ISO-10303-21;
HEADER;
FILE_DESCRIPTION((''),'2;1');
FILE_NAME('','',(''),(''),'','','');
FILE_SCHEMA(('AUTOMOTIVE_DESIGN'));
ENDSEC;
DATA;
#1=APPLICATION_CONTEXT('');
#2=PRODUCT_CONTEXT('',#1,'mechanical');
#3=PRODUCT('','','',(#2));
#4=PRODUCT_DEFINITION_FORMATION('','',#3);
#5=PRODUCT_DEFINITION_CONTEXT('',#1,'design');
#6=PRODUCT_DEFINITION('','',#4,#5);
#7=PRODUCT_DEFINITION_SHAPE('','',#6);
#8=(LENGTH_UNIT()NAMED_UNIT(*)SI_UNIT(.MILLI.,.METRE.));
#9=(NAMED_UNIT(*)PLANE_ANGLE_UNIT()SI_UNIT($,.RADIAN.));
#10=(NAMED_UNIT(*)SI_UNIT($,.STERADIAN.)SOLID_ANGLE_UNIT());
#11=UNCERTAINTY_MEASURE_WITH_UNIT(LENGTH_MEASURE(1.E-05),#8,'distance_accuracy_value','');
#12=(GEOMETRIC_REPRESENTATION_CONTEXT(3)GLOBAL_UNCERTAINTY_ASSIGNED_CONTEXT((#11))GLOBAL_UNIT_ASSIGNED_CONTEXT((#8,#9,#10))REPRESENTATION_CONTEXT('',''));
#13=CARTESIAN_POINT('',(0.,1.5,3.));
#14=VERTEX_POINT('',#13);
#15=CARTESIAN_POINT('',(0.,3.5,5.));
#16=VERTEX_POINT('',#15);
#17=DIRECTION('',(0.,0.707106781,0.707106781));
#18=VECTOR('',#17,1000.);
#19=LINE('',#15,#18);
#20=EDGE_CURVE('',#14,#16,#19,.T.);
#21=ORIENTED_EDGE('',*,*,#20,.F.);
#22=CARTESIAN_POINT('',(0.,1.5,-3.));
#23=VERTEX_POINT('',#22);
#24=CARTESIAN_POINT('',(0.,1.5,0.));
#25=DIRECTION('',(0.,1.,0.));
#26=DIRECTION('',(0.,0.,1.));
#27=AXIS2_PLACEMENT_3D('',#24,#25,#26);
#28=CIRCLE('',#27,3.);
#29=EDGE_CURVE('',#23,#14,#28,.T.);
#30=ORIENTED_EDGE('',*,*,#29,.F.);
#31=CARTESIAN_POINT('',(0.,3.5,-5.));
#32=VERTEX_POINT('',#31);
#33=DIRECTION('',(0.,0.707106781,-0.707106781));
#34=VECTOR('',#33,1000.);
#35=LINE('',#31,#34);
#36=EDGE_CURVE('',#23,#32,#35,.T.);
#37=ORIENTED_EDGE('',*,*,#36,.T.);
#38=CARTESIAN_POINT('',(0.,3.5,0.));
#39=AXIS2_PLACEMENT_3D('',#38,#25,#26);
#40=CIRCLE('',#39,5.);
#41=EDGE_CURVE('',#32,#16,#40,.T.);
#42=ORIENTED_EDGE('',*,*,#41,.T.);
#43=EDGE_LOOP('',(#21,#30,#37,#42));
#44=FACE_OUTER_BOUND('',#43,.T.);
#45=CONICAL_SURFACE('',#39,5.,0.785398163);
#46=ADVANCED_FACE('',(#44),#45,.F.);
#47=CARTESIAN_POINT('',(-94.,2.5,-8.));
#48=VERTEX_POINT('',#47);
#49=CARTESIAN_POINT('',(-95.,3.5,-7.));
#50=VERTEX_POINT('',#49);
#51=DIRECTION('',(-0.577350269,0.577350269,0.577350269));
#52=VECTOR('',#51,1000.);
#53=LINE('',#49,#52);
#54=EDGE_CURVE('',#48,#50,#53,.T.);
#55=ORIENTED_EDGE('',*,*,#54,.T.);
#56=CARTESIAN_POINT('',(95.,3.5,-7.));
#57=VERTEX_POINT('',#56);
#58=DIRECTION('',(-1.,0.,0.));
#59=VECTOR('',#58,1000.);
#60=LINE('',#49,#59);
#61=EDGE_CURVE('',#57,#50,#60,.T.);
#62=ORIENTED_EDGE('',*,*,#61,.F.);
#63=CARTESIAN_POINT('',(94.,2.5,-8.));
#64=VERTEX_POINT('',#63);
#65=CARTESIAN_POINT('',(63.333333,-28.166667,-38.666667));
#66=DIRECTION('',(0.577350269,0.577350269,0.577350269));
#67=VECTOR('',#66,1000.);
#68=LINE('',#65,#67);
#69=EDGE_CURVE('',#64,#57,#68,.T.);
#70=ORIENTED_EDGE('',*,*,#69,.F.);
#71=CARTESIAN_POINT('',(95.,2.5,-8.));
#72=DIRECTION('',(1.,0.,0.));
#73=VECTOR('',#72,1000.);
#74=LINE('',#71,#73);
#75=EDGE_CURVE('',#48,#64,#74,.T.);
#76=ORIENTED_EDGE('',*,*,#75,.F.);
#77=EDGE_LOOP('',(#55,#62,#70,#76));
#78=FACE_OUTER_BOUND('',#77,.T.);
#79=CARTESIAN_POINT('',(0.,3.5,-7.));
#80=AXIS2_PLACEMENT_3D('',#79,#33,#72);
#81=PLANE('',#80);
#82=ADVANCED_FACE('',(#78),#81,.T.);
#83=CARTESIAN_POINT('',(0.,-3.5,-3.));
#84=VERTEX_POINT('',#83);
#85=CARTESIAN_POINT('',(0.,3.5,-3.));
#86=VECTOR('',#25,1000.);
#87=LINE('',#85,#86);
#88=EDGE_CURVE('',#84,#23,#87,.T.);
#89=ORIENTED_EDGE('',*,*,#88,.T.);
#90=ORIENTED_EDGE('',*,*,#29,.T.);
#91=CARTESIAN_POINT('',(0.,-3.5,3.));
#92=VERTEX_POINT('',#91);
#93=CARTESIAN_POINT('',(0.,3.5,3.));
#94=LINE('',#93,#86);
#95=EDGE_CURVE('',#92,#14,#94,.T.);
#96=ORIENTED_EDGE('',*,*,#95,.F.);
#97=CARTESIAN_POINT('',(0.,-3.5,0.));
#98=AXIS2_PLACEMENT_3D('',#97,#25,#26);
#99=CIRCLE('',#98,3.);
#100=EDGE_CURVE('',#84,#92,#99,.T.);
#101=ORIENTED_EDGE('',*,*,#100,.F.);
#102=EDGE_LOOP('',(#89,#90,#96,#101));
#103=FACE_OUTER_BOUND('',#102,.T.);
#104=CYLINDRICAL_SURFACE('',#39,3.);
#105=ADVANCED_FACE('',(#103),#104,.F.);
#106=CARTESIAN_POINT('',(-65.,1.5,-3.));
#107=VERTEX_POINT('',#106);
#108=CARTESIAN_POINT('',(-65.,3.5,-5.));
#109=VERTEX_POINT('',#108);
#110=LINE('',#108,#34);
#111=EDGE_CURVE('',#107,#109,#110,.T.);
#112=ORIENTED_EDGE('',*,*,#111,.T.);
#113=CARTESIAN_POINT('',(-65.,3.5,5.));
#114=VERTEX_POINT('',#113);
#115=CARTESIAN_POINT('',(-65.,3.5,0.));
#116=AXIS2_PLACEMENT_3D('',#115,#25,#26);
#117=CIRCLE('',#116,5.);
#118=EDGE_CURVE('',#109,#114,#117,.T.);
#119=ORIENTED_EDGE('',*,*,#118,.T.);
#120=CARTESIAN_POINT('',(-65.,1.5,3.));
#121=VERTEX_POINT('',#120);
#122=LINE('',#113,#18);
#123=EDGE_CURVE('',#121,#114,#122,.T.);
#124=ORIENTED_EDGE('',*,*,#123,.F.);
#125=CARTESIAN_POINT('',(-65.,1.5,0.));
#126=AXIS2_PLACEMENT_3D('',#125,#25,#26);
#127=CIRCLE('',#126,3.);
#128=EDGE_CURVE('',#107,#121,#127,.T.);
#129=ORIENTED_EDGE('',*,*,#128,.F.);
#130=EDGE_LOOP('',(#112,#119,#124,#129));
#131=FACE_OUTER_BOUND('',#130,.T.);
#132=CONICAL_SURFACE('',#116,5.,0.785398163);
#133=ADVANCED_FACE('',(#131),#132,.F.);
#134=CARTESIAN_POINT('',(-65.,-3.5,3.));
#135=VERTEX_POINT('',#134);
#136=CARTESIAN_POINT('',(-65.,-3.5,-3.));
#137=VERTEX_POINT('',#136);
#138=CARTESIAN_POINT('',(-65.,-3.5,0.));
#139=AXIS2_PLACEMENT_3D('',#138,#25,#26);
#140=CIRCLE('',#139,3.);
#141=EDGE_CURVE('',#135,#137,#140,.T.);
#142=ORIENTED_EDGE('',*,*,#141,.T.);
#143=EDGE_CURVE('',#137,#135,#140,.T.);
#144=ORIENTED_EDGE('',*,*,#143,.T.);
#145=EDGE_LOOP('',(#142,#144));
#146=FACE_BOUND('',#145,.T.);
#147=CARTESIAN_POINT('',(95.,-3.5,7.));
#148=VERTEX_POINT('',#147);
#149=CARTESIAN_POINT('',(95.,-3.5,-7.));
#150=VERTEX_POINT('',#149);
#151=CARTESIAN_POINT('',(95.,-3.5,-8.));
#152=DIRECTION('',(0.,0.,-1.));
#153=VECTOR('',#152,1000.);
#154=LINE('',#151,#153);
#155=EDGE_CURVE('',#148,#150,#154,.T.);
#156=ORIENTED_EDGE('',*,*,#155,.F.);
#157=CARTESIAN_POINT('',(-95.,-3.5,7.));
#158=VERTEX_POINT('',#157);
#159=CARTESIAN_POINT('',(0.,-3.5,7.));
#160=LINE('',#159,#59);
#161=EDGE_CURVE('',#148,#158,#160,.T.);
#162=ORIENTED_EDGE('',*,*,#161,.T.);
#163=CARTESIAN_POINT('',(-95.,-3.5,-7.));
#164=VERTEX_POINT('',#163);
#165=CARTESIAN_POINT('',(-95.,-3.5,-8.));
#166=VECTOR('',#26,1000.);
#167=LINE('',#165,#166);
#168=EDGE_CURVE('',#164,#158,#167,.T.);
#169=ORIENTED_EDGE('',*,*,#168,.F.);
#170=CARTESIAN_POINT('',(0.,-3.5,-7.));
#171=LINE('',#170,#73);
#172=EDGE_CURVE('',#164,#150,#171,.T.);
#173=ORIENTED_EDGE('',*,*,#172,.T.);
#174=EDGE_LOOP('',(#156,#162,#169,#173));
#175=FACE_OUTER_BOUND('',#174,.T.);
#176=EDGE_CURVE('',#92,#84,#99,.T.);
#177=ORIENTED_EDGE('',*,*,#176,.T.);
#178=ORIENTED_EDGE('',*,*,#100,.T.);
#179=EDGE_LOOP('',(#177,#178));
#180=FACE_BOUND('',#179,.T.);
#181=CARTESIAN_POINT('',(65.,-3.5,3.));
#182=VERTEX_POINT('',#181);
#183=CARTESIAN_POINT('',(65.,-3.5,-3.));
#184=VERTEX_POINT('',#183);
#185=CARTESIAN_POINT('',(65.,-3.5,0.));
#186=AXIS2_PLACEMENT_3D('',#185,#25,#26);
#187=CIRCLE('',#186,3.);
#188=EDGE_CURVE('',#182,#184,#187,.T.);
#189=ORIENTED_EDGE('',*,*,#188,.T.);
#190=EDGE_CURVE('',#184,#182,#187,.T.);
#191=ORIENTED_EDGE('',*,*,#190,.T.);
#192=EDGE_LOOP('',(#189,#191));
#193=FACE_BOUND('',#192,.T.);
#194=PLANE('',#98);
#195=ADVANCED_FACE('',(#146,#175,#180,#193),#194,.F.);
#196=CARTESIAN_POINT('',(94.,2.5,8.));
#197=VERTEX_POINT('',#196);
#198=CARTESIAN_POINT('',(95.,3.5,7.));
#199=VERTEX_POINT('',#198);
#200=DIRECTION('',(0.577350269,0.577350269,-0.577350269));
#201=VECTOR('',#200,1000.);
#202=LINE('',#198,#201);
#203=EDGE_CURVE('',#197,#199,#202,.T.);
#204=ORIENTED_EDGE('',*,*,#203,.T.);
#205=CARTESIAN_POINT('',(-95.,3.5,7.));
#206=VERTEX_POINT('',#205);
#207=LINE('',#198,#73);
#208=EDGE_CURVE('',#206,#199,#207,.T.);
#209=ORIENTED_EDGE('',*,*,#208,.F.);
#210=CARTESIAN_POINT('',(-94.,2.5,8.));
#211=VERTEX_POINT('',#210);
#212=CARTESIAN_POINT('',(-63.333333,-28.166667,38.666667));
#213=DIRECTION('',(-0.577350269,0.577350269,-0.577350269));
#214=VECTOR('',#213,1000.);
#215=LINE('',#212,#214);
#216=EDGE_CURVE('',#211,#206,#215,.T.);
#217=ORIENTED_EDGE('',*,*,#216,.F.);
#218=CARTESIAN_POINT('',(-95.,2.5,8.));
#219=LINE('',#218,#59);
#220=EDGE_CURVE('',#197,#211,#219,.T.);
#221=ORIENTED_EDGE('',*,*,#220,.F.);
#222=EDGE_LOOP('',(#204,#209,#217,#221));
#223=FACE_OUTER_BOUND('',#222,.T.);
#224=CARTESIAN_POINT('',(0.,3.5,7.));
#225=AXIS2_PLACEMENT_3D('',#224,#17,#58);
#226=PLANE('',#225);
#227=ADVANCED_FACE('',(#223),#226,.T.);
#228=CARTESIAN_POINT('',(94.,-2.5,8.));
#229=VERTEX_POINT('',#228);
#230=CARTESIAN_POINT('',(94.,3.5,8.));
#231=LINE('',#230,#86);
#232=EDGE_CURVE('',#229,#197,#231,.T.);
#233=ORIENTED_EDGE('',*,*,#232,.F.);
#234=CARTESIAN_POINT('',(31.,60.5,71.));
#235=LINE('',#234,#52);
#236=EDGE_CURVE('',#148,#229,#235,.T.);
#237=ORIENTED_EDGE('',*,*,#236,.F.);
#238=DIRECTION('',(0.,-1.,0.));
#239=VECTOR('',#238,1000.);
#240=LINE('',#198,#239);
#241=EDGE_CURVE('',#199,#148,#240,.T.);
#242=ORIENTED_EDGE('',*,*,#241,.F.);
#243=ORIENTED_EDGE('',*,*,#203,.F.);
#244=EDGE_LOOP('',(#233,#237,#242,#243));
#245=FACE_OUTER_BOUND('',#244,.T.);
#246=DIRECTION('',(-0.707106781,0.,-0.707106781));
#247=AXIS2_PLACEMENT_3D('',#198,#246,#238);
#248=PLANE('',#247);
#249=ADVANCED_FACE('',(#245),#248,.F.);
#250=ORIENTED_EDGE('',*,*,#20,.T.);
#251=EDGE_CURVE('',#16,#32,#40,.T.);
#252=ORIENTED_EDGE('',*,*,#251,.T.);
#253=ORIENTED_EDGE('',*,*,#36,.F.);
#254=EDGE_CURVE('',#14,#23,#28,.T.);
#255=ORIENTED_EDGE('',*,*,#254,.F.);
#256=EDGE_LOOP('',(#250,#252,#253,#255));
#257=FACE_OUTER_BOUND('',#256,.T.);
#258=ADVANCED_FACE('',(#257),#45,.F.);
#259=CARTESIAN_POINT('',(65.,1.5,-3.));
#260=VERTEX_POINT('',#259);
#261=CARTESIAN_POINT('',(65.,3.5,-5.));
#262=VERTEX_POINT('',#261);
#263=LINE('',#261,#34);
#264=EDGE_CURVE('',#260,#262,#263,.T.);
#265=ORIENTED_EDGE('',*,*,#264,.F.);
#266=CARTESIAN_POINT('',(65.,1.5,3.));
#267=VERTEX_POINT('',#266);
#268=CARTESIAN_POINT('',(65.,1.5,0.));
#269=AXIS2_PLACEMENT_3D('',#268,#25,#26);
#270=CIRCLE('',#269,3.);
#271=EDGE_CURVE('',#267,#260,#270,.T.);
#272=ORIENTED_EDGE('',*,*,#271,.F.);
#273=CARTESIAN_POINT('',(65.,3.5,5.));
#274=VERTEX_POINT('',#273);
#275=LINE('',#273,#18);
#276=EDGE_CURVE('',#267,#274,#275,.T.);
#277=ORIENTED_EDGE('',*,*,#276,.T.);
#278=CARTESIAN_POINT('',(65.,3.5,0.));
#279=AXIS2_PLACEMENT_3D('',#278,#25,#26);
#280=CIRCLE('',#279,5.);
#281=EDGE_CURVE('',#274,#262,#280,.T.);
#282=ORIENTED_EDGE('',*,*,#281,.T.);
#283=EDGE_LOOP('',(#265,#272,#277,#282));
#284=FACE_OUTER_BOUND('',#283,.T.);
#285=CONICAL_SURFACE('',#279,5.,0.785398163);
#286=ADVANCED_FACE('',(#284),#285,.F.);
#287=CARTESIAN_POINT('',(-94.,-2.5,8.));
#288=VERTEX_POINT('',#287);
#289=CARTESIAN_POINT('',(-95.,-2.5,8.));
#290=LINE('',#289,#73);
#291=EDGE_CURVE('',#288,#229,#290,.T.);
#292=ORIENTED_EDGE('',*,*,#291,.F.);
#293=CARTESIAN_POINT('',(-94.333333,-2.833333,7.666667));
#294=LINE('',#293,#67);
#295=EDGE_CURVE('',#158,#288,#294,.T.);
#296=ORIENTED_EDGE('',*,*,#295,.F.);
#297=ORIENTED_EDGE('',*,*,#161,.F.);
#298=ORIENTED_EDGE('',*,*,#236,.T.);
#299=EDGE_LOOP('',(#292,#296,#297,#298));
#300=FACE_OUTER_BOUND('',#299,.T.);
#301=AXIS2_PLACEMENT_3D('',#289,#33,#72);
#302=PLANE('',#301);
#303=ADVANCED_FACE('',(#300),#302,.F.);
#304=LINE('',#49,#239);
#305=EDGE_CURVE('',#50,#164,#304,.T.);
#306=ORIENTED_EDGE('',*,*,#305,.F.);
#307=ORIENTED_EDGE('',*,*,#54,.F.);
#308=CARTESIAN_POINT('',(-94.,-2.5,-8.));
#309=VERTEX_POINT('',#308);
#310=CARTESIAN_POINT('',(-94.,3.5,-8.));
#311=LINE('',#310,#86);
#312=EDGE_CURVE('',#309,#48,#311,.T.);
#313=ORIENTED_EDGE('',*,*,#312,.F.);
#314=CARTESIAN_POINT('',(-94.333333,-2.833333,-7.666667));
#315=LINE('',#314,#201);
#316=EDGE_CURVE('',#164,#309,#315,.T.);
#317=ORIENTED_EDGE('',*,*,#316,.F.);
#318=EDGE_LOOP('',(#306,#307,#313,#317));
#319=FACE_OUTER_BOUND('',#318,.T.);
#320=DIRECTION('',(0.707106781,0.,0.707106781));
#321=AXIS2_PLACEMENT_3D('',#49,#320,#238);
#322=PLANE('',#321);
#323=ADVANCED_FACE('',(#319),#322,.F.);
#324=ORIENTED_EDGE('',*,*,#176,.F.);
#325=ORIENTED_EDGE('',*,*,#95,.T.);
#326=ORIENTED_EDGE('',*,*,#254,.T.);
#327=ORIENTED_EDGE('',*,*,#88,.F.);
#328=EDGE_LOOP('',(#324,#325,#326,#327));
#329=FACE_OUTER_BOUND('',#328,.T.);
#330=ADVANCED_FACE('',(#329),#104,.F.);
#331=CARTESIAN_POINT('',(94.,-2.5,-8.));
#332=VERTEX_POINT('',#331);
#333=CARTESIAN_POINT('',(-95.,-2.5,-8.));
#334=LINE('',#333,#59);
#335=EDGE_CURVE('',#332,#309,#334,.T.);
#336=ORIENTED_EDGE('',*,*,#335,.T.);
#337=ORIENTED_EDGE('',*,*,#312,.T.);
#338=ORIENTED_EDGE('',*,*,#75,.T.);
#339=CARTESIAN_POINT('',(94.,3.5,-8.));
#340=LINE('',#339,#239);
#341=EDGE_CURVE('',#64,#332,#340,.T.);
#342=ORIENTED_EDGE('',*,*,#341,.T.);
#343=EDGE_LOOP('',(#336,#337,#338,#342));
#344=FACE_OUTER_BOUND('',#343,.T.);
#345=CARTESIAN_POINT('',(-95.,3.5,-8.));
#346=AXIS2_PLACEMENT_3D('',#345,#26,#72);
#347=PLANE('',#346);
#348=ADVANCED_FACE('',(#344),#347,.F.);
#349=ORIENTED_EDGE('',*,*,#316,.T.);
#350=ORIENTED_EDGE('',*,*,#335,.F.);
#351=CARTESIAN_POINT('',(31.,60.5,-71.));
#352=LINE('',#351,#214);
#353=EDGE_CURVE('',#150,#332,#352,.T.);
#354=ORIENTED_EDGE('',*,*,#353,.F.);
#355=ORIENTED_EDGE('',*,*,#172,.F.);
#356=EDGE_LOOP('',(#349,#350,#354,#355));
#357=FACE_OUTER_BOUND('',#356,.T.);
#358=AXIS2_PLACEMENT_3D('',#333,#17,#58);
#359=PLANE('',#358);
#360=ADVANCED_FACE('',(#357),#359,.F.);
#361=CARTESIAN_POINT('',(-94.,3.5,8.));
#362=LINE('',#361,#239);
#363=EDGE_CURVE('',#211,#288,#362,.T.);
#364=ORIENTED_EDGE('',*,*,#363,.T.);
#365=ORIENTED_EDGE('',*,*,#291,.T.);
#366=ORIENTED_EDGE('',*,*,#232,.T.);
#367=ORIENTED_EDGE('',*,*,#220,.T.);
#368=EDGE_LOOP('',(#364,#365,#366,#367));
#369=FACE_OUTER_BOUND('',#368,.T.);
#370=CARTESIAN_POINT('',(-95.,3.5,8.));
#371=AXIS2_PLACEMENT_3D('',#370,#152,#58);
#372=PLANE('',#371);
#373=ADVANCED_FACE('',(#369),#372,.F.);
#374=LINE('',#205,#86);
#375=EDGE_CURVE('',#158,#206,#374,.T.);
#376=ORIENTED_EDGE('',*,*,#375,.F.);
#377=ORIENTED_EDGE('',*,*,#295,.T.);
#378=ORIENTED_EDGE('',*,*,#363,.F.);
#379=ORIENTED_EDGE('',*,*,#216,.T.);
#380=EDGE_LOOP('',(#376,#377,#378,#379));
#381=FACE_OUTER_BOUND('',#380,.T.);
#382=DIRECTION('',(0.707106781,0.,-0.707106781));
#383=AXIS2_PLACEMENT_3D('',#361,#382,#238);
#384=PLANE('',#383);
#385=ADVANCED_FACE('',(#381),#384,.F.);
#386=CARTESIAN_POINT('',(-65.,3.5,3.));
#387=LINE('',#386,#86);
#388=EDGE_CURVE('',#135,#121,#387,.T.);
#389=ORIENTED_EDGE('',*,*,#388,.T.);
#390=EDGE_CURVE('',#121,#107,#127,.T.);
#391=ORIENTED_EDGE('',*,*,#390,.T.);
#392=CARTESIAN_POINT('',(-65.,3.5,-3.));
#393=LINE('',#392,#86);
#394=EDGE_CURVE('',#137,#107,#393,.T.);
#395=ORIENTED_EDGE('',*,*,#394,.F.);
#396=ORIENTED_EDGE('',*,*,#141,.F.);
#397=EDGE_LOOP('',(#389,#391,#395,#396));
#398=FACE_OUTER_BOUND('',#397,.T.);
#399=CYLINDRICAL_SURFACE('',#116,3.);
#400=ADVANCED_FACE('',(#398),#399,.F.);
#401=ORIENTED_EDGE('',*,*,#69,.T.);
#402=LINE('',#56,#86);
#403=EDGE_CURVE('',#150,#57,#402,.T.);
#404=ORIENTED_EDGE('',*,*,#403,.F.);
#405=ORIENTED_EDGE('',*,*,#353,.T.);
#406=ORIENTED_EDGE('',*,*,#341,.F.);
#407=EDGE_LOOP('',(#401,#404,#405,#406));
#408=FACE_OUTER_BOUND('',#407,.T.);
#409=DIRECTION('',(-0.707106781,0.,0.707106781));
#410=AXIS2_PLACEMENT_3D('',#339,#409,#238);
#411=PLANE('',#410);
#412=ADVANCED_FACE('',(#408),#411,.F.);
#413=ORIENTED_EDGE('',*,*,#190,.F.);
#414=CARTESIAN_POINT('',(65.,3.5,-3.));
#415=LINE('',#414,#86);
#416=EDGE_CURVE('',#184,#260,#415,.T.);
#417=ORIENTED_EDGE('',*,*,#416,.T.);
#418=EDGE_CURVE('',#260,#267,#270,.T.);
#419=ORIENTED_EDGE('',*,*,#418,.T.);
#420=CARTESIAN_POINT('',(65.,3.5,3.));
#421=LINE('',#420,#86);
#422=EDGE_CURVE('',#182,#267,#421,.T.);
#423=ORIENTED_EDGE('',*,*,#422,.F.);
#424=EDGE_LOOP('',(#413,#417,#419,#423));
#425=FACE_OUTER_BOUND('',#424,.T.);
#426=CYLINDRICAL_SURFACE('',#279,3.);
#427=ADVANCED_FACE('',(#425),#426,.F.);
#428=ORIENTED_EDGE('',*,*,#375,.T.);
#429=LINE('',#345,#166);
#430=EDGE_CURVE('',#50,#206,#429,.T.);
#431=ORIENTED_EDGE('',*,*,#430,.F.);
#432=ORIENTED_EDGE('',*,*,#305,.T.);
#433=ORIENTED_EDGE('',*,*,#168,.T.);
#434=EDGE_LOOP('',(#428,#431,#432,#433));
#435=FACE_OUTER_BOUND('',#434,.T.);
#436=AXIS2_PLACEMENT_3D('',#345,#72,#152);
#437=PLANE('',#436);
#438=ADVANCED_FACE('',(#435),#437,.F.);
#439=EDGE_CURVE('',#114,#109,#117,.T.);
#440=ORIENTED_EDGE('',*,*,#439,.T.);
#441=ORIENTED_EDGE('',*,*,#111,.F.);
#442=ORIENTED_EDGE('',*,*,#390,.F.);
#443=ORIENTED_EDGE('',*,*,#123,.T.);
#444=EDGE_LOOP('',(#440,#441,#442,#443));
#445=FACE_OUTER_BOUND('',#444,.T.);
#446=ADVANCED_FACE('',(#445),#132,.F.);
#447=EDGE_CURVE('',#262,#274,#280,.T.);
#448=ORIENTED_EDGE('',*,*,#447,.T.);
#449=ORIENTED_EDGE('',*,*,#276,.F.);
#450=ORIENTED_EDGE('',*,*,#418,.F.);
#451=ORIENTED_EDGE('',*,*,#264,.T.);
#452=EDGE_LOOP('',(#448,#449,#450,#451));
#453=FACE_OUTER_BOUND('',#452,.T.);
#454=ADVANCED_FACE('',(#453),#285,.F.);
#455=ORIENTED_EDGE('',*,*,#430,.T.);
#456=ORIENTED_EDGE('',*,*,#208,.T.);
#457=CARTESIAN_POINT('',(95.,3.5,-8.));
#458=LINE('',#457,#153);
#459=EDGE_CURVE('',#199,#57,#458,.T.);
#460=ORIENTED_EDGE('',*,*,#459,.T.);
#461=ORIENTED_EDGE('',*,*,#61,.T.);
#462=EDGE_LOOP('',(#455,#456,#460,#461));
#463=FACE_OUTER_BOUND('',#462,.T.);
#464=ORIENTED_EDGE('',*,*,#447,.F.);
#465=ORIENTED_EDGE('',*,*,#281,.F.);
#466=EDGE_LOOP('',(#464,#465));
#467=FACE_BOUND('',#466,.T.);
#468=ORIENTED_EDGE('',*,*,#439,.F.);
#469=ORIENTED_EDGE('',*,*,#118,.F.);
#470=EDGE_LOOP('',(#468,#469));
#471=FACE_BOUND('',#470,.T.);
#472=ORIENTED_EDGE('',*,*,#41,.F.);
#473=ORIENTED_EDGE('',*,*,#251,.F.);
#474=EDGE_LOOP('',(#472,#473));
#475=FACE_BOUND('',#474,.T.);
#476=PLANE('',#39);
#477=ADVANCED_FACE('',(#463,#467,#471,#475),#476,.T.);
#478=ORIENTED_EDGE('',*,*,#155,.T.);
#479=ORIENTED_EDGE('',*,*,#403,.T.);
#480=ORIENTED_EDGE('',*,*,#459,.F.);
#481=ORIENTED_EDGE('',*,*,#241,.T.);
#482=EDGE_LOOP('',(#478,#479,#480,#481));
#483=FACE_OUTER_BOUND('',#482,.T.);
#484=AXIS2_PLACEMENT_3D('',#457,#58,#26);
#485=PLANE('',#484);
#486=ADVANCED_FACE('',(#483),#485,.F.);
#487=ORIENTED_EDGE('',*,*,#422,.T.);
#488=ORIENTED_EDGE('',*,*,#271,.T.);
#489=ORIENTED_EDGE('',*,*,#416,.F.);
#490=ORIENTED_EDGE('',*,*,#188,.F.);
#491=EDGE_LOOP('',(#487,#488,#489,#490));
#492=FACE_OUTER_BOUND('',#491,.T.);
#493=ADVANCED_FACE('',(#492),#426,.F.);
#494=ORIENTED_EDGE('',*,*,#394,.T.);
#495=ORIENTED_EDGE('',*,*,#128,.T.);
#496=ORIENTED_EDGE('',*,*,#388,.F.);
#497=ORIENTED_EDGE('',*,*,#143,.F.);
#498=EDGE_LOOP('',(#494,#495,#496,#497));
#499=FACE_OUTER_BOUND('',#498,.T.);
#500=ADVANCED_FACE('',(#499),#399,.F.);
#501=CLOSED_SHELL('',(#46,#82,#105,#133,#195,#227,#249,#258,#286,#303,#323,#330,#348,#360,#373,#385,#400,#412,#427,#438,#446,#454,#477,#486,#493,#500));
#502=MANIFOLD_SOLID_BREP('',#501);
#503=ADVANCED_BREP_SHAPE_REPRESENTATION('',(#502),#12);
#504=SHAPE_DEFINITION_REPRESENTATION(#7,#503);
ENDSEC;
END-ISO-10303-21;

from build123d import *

# Parameters (mm, degrees)
SKETCH1_W           = 190
SKETCH1_H           = 16
BOSS_EXTRUDE1_DEPTH = 3.5
HOLE1_D             = 6
HOLE1_DEPTH         = 20
HOLE1_CSINK_D       = 10
HOLE1_CSINK_ANGLE   = 90
CHAMFER1_SIZE       = 1


with BuildPart() as part:
    # Sketch1 → Boss-Extrude1 (new, symmetric)
    with BuildSketch(Plane(origin=(0, 0, 0), x_dir=(1, 0, 0), z_dir=(0, 1, 0))):
        Rectangle(SKETCH1_W, SKETCH1_H)
    extrude(amount=BOSS_EXTRUDE1_DEPTH, both=True)

    # Hole1
    with Locations(Plane(origin=(0, 3.5, 0), x_dir=(1, 0, 0), z_dir=(0, 1, 0))):
        with Locations((-65, 0), (0, 0), (65, 0)):
            CounterSinkHole(HOLE1_D / 2, HOLE1_CSINK_D / 2, depth=HOLE1_DEPTH, counter_sink_angle=HOLE1_CSINK_ANGLE)

    # Chamfer1
    chamfer1_edges = [part.edges().sort_by_distance(p)[0] for p in [
        (0, 3.5, 8),
        (0, -3.5, 8),
        (0, -3.5, -8),
        (95, 0, 8),
        (-95, 0, 8),
        (-95, 0, -8),
        (95, 0, -8),
        (0, 3.5, -8),
    ]]
    chamfer(chamfer1_edges, length=CHAMFER1_SIZE)


solid = part.part
